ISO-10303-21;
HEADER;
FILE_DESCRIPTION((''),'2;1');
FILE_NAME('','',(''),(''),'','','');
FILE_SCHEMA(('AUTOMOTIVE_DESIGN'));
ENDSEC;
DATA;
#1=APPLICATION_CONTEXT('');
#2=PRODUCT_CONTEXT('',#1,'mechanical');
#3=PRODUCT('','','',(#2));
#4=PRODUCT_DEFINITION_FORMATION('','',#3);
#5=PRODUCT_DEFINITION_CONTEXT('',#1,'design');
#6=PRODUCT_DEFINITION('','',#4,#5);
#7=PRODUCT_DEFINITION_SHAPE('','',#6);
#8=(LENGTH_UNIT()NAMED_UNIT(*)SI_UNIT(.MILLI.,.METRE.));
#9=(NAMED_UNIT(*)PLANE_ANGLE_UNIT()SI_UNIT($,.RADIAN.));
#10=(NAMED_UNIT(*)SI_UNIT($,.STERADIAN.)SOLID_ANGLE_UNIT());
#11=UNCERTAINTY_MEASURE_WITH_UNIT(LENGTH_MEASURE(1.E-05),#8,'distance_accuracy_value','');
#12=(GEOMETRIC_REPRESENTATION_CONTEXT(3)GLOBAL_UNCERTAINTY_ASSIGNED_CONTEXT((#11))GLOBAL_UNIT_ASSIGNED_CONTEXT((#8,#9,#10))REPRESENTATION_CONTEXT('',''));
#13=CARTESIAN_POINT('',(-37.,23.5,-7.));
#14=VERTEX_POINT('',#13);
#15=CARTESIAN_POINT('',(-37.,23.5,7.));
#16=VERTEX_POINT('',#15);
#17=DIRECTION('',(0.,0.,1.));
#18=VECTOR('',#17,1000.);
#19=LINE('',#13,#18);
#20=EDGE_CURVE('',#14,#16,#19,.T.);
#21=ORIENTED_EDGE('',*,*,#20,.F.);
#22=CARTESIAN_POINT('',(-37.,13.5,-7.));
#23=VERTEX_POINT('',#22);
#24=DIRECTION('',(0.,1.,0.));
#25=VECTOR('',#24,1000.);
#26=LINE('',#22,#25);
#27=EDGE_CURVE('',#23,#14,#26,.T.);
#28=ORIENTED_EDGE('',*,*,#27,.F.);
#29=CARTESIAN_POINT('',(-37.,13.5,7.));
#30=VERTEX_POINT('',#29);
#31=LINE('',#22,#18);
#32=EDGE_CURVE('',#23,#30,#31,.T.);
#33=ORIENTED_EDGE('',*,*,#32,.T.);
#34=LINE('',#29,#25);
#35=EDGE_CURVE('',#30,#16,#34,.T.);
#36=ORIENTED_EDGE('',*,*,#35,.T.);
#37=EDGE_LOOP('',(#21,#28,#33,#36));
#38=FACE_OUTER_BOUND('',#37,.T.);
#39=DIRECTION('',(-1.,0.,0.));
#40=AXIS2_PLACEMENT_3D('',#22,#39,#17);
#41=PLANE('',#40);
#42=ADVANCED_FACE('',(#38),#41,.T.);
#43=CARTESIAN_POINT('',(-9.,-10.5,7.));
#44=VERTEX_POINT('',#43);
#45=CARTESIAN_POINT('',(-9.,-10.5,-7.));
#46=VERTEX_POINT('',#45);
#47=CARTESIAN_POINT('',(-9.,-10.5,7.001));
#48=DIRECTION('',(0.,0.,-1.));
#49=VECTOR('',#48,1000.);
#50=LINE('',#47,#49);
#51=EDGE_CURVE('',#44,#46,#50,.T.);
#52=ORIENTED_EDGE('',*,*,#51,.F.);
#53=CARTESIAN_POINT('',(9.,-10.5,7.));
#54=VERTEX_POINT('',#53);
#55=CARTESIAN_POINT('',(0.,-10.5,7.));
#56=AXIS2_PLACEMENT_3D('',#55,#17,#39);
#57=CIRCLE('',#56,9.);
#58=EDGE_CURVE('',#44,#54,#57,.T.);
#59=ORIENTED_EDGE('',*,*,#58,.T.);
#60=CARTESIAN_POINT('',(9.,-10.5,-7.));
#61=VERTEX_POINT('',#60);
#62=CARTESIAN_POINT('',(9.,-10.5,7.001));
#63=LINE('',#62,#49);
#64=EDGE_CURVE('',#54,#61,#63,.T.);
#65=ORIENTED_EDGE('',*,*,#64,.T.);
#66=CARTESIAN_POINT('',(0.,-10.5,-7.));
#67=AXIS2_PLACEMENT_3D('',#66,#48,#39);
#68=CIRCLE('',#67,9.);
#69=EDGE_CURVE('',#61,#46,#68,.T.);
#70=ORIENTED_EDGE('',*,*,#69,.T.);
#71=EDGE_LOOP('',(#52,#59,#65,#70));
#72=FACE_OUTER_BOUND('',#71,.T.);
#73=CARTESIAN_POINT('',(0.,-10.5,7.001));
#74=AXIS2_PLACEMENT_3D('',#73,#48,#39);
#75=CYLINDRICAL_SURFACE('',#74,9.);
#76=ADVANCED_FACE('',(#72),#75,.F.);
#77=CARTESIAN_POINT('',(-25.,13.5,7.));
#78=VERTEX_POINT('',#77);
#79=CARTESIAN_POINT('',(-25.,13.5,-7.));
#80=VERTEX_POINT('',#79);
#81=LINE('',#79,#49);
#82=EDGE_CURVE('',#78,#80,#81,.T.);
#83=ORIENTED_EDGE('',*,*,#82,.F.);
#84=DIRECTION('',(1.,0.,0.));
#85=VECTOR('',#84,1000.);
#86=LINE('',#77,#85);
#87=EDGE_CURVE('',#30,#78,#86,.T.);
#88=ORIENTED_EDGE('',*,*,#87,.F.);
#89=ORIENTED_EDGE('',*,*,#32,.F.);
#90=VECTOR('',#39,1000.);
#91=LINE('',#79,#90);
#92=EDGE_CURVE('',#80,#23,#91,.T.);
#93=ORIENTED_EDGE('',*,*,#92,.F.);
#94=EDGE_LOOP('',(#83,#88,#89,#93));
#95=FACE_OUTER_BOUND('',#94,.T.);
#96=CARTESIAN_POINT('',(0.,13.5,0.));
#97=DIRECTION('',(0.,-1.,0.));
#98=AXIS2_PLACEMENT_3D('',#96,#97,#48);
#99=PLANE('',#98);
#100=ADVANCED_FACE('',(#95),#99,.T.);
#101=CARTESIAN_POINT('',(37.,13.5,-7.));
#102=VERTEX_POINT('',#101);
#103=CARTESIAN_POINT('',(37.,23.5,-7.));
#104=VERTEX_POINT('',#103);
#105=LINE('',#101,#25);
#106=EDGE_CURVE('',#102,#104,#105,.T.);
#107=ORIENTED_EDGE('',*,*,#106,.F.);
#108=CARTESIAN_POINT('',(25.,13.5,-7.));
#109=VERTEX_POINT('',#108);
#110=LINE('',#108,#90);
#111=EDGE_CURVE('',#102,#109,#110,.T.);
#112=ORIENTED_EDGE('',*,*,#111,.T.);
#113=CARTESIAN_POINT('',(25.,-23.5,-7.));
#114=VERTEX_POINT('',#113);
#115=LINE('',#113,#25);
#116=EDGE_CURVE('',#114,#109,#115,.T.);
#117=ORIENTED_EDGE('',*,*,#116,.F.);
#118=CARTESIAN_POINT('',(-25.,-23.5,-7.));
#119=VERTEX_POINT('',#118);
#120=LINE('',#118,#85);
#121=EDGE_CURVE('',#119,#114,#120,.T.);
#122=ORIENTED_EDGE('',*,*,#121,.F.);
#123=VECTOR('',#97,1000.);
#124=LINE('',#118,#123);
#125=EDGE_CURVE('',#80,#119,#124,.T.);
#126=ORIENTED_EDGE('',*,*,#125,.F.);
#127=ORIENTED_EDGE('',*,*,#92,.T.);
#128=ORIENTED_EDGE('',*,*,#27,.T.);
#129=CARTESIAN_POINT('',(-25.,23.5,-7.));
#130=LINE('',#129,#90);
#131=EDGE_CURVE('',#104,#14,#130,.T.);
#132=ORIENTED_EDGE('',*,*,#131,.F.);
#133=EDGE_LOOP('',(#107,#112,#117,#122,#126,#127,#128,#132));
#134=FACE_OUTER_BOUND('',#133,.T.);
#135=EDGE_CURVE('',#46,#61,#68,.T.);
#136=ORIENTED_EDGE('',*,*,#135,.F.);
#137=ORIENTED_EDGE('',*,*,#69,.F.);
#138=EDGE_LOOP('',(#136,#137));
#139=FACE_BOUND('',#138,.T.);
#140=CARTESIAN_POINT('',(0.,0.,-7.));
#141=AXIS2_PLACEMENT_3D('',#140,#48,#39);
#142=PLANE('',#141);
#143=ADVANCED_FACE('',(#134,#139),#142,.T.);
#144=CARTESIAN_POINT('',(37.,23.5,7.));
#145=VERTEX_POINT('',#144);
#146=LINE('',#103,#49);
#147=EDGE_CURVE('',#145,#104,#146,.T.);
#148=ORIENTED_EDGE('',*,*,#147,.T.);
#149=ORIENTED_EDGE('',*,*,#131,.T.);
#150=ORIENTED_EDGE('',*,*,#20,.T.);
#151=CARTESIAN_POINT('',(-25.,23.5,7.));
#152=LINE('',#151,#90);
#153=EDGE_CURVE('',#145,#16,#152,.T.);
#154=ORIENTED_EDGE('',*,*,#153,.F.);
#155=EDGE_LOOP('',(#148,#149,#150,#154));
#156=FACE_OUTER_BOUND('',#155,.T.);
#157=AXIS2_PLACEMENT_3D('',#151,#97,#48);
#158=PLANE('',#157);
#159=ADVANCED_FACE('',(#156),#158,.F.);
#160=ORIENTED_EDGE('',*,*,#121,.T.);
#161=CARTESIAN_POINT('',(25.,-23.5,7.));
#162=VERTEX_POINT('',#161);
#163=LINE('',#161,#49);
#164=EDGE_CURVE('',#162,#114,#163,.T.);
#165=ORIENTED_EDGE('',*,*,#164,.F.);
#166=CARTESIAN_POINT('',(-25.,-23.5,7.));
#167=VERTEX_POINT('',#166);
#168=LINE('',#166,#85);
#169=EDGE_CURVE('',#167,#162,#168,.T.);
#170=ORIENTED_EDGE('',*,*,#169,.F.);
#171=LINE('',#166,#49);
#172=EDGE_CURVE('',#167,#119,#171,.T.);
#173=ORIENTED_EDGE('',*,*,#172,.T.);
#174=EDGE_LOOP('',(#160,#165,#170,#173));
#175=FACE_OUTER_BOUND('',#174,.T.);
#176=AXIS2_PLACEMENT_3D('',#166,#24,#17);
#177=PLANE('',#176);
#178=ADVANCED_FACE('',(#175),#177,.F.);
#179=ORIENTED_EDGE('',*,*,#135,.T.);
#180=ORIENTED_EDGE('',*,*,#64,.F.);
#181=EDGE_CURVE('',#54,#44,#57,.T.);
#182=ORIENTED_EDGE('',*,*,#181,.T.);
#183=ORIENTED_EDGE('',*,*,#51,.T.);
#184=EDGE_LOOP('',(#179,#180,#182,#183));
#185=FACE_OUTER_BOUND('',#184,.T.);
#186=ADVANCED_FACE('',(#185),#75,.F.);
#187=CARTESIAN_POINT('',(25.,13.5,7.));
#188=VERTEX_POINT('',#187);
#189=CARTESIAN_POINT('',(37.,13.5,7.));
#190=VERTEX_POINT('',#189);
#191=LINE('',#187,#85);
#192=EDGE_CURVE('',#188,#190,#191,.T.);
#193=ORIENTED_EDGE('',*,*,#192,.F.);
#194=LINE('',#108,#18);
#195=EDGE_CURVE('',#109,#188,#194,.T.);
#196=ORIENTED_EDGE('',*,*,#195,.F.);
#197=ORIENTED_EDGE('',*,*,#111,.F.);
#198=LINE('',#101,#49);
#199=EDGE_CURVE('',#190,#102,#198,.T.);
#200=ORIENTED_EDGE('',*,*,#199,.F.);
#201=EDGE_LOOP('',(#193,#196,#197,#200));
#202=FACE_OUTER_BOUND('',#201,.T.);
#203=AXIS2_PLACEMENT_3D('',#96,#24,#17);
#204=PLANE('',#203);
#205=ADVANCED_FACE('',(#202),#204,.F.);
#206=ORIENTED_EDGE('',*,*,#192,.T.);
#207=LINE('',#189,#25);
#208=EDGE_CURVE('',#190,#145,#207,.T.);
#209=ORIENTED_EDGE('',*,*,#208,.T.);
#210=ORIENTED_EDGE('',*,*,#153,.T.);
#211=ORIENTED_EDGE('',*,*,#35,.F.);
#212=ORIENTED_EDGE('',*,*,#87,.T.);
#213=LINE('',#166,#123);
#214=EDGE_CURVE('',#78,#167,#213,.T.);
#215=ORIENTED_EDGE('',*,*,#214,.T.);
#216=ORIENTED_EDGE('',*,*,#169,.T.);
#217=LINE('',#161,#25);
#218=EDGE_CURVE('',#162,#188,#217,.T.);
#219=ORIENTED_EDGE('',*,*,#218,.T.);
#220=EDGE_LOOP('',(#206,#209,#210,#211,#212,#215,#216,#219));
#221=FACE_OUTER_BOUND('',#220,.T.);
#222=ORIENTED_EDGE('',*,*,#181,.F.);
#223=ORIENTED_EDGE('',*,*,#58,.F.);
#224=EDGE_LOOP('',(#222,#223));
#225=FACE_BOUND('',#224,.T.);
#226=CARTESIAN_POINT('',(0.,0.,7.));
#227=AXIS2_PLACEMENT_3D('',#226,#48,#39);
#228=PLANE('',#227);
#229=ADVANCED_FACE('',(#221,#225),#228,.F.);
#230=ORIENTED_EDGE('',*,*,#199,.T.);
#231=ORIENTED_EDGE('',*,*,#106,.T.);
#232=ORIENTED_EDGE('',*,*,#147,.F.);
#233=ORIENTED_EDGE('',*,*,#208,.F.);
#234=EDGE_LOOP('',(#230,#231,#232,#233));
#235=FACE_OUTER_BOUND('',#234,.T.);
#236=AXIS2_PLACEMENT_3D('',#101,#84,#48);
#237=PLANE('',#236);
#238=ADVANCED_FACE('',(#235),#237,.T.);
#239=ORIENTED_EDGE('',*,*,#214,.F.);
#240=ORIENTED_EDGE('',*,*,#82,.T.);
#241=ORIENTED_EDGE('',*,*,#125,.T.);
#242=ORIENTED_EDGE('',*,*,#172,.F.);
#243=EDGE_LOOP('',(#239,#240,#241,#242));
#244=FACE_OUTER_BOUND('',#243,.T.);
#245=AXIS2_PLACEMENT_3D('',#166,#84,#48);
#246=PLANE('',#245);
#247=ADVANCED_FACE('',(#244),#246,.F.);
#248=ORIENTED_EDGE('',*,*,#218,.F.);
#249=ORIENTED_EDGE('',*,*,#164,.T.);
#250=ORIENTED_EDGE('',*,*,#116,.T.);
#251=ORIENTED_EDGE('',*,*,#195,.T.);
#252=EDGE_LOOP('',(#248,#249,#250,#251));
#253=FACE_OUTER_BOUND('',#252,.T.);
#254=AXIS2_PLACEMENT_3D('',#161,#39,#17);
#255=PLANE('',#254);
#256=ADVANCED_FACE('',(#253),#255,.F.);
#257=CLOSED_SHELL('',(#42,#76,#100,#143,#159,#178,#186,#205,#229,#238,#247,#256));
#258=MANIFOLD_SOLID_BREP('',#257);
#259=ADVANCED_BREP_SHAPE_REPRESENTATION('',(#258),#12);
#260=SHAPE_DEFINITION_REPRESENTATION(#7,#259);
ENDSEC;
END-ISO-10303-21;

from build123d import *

# Parameters (mm, degrees)
SKETCH_1_W          = 50
SKETCH_1_H          = 47
EXTRUDE_1_DEPTH     = 7
CUT_EXTRUDE_1_REACH = 39.057
SKETCH_2_R          = 9
SKETCH_4_W          = 12
SKETCH_4_H          = 14
EXTRUDE_2_DEPTH     = 10


with BuildPart() as part:
    # 草图1 → 凸台-拉伸1 (new, symmetric)
    with BuildSketch(Plane.XY):
        Rectangle(SKETCH_1_W, SKETCH_1_H)
    extrude(amount=EXTRUDE_1_DEPTH, both=True)

    # 草图2 → 切除-拉伸1 (cut, up to next)
    with BuildSketch(Plane(origin=(0, 0, -7), x_dir=(-1, 0, 0), z_dir=(0, 0, -1)), mode=Mode.PRIVATE) as cut_extrude_1_sk1:
        with Locations((0, -10.5)):
            Circle(SKETCH_2_R)
    cut_extrude_1_tool1 = extrude(cut_extrude_1_sk1.sketch, amount=-CUT_EXTRUDE_1_REACH, mode=Mode.PRIVATE) & part.part
    add(cut_extrude_1_tool1.solids().sort_by_distance((0, -10.5, -7))[0], mode=Mode.SUBTRACT)

    # 草图4 → 凸台-拉伸2 (add)
    with BuildSketch(Plane(origin=(0, 23.5, 0), x_dir=(1, 0, 0), z_dir=(0, 1, 0))):
        with Locations((31, 0)):
            Rectangle(SKETCH_4_W, SKETCH_4_H)
        with Locations((-31, 0)):
            Rectangle(SKETCH_4_W, SKETCH_4_H)
    extrude(amount=-EXTRUDE_2_DEPTH)


solid = part.part
